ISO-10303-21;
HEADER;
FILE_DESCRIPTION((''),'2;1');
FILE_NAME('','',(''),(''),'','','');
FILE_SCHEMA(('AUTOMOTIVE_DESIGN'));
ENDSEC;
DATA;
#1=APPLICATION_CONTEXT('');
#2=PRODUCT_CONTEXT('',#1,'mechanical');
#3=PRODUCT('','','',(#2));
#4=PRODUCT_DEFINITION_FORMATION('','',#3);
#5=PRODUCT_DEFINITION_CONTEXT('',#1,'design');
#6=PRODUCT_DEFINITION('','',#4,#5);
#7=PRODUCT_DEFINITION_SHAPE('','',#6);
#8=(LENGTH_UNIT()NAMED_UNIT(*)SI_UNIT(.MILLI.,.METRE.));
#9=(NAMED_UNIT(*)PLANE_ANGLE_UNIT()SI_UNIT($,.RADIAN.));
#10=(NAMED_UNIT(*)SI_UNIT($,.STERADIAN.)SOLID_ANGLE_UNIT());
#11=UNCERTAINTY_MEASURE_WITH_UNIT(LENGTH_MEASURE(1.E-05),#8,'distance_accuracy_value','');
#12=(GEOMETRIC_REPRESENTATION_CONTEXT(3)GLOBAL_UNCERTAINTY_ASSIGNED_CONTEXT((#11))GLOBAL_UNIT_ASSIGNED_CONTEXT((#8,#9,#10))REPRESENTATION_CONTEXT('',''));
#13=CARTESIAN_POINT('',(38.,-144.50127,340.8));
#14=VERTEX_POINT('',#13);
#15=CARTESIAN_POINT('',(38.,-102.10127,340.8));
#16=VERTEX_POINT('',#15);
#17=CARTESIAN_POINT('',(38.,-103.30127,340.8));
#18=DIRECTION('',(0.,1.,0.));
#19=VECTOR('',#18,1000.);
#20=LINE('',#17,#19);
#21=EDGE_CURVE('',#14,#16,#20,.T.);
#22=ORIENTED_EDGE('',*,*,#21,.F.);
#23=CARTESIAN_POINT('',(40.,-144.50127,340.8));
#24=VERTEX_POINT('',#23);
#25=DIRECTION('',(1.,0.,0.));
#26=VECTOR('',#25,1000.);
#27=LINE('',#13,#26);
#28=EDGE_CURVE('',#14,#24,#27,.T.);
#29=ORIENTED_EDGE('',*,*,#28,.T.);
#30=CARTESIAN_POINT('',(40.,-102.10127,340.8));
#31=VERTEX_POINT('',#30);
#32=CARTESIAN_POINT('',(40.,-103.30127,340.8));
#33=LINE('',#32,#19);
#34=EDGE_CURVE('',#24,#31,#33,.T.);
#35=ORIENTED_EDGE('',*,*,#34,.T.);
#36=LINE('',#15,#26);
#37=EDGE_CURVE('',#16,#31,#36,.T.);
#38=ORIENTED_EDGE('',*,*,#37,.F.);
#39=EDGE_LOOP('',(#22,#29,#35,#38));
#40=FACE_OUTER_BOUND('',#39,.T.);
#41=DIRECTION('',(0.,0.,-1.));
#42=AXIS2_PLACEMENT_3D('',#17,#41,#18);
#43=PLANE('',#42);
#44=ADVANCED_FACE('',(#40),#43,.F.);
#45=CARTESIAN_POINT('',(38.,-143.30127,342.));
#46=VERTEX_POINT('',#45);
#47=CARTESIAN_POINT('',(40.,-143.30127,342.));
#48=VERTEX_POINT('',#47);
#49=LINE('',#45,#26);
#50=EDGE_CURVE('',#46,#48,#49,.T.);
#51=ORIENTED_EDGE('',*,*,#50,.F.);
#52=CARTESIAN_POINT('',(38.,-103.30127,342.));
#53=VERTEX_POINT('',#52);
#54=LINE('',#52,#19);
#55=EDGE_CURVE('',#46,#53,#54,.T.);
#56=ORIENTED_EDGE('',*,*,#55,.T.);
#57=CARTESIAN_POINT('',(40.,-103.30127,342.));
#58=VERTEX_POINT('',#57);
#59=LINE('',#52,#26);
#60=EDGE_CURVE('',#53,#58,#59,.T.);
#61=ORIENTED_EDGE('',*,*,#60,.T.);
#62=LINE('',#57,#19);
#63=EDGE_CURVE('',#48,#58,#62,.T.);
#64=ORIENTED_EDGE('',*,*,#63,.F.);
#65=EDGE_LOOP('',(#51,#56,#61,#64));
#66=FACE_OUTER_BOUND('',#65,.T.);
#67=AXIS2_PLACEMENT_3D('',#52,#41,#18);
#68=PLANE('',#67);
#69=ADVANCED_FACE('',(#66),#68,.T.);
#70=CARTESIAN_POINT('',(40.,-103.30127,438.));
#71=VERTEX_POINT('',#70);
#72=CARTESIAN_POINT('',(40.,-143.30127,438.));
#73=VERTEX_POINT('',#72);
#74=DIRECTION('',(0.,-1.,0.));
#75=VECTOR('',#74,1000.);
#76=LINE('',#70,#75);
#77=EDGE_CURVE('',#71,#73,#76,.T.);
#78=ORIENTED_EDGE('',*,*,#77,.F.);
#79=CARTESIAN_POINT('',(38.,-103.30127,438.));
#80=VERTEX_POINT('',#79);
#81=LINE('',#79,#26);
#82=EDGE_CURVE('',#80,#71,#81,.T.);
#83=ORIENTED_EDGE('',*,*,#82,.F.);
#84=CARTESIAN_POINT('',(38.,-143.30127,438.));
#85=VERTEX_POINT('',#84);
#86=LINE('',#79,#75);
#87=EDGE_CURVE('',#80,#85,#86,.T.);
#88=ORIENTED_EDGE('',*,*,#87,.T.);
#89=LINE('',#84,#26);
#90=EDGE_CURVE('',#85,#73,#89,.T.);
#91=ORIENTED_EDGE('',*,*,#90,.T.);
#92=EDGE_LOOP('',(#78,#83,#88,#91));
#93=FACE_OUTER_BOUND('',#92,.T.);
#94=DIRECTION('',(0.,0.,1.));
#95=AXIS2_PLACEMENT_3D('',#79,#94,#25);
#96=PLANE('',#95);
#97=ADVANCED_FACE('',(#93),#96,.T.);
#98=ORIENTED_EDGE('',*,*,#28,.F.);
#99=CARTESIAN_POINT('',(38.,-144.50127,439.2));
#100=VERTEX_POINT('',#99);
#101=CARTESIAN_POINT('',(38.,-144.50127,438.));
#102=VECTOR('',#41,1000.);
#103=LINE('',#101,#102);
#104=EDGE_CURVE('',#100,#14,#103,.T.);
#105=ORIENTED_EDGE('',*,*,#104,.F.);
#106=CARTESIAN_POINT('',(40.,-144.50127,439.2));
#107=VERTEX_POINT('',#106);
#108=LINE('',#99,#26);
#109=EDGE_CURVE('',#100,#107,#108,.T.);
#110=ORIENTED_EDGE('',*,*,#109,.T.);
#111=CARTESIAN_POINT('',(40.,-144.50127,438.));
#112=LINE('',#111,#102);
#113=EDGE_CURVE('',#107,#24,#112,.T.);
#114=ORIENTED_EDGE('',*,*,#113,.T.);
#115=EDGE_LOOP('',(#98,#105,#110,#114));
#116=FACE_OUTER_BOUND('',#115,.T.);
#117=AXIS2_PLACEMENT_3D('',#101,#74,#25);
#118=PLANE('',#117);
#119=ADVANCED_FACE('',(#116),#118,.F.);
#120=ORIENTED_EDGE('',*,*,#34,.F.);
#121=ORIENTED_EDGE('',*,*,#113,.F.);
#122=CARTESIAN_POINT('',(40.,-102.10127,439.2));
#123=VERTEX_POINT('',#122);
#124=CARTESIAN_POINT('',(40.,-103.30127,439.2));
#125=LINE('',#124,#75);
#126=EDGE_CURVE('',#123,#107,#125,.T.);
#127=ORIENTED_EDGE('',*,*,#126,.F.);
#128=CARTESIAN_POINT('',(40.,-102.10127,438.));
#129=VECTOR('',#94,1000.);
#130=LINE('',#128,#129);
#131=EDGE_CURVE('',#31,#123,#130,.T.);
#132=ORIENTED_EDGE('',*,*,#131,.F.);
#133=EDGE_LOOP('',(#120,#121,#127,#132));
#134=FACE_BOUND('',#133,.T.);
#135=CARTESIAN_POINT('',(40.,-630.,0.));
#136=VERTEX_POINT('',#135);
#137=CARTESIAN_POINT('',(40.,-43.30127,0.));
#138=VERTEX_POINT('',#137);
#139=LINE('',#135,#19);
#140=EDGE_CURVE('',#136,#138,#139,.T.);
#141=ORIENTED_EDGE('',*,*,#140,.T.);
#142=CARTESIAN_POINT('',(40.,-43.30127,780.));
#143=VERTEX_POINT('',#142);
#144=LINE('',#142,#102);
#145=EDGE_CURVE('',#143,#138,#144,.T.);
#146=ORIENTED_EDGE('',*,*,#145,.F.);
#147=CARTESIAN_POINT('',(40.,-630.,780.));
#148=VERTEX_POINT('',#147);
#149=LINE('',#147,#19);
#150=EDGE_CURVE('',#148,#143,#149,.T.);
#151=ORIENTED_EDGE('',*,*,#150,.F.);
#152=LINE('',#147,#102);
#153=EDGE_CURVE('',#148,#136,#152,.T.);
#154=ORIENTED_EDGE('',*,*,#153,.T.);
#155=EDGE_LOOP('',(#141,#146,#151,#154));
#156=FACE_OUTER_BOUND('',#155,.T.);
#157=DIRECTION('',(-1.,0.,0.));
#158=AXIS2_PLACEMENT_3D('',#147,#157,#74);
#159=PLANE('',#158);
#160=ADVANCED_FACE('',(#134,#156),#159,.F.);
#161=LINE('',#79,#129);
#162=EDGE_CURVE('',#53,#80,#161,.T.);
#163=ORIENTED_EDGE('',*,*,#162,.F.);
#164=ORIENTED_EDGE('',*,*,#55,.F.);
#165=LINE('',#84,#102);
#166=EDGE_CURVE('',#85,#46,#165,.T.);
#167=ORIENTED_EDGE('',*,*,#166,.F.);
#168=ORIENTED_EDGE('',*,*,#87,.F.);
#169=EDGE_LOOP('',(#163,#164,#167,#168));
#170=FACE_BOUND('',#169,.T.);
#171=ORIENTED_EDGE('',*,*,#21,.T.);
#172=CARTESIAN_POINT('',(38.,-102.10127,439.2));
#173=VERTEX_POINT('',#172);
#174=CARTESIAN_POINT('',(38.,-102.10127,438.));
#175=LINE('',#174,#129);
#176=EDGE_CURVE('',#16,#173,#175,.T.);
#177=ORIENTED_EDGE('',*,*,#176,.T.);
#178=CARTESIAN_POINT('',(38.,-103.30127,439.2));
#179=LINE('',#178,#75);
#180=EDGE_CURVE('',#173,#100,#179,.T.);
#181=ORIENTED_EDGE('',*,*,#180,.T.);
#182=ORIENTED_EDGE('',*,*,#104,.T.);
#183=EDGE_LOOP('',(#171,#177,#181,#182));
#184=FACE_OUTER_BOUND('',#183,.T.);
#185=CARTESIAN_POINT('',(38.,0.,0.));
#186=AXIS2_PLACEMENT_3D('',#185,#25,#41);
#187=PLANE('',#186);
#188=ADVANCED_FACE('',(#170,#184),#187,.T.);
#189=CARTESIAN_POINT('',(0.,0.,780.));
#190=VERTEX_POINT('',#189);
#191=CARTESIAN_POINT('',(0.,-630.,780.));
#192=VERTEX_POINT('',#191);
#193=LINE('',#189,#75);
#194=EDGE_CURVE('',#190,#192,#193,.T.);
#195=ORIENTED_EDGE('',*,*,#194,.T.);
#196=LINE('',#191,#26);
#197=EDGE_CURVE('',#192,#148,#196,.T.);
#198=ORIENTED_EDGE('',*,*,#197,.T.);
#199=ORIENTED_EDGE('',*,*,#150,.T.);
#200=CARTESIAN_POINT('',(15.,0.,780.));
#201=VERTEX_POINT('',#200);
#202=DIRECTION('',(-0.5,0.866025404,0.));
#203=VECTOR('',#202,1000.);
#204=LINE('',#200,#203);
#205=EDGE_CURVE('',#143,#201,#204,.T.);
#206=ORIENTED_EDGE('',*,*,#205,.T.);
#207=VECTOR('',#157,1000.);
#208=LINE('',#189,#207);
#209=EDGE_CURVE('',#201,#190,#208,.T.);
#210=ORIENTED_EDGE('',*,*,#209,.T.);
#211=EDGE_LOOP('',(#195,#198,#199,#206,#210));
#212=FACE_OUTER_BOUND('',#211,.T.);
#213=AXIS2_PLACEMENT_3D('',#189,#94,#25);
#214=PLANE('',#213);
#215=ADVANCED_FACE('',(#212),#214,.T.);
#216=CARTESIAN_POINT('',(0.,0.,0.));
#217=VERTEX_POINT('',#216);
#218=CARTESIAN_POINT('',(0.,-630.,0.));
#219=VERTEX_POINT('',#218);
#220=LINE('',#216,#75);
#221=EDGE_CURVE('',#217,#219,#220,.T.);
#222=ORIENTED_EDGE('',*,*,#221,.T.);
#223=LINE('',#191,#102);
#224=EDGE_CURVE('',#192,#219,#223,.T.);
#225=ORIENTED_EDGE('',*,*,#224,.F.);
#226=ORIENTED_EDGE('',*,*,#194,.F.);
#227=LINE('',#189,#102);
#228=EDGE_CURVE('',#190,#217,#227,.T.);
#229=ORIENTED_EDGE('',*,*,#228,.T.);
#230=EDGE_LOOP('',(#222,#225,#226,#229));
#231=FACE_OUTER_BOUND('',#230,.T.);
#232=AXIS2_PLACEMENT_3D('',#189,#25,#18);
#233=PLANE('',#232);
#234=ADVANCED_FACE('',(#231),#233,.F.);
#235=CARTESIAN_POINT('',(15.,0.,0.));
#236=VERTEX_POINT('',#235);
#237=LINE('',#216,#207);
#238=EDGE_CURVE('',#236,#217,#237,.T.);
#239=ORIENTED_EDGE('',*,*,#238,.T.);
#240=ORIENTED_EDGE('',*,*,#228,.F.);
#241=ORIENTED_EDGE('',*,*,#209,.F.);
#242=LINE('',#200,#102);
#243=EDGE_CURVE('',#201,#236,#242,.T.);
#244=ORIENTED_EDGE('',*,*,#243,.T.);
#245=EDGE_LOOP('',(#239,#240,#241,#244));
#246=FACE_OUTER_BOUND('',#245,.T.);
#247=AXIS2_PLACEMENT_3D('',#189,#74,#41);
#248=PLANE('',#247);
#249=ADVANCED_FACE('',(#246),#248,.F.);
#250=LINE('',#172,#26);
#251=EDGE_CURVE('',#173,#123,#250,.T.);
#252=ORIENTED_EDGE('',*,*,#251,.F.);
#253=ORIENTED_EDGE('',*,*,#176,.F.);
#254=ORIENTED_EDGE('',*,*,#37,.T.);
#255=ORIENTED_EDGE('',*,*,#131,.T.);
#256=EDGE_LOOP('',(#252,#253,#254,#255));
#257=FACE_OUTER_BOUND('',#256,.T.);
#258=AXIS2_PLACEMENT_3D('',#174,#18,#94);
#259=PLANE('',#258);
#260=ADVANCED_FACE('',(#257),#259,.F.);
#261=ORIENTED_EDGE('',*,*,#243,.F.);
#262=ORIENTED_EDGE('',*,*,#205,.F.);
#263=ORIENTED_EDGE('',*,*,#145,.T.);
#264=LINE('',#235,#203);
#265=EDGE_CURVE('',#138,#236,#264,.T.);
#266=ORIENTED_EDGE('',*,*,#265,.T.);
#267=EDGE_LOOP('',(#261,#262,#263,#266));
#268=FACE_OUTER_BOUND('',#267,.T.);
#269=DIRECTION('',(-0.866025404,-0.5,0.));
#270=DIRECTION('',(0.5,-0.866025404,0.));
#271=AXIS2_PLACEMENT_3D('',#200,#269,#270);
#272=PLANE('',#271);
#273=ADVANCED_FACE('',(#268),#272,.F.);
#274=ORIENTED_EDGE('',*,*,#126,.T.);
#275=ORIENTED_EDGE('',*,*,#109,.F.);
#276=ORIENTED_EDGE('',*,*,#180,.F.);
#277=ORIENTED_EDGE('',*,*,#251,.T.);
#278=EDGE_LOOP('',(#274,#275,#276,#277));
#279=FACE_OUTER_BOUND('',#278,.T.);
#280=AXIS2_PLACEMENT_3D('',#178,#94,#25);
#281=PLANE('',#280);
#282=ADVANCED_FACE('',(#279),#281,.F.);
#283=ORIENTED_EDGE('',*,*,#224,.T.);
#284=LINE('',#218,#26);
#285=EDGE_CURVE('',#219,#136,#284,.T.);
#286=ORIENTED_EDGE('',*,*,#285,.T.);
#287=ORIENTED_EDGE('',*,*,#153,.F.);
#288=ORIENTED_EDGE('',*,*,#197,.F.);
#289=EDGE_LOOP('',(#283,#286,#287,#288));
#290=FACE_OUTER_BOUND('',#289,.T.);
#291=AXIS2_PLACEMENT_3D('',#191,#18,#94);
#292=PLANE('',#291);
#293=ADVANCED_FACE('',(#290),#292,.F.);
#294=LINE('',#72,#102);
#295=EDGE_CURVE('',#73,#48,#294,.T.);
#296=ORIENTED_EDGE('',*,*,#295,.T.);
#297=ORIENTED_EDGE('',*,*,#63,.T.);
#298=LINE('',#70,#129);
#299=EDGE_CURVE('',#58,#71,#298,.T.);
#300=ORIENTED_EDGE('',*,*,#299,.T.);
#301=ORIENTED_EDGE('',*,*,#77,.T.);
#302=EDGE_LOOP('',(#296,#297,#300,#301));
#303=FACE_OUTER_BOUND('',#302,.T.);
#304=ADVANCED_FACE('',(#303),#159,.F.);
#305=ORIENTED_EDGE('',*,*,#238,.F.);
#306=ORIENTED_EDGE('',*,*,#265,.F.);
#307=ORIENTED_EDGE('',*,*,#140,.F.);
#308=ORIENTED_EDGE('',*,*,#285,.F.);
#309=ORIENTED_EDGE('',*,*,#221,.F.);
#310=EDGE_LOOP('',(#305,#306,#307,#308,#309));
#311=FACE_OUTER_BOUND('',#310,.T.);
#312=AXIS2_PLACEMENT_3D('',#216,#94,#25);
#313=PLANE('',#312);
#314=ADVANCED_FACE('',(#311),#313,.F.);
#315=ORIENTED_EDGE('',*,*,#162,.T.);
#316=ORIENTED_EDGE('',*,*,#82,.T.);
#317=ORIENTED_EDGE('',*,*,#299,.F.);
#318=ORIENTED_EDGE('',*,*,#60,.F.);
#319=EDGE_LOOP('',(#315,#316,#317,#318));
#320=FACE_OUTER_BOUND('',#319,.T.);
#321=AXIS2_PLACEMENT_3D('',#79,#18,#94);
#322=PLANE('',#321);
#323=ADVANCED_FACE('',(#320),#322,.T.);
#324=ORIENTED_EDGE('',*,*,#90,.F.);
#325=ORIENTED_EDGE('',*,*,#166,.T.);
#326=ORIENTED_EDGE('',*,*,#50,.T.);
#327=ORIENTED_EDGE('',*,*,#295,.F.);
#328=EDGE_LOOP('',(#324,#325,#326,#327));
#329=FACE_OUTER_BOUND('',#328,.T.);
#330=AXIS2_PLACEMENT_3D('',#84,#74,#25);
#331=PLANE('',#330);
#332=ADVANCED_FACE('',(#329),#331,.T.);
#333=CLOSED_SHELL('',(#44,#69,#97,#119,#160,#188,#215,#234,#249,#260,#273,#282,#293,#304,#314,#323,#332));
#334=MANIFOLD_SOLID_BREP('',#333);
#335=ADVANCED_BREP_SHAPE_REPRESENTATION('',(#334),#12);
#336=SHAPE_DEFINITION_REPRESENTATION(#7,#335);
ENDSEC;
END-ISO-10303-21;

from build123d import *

# Parameters (mm, degrees)
BOSS_EXTRUDE1_DEPTH     = 780
SKETCH2_W               = 98.4
SKETCH2_H               = 42.4
SKETCH2_W_2             = 96
SKETCH2_H_2             = 40
CUT_EXTRUDE_THIN1_DEPTH = 2


with BuildPart() as part:
    # Sketch1 → Boss-Extrude1 (new body)
    with BuildSketch(Plane.XY):
        Polygon((0, 0), (0, -630), (40, -630), (40, -43.301270189), (15, 0), align=None)
    extrude(amount=BOSS_EXTRUDE1_DEPTH)

    # Sketch2 → Cut-Extrude-Thin1 (cut)
    with BuildSketch(Plane(origin=(40, 0, 0), x_dir=(0, 0, -1), z_dir=(1, 0, 0))):
        with Locations((-390, -123.301270189)):
            Rectangle(SKETCH2_W, SKETCH2_H)
        with Locations((-390, -123.301270189)):
            Rectangle(SKETCH2_W_2, SKETCH2_H_2, mode=Mode.SUBTRACT)
    extrude(amount=-CUT_EXTRUDE_THIN1_DEPTH, mode=Mode.SUBTRACT)


solid = part.part
